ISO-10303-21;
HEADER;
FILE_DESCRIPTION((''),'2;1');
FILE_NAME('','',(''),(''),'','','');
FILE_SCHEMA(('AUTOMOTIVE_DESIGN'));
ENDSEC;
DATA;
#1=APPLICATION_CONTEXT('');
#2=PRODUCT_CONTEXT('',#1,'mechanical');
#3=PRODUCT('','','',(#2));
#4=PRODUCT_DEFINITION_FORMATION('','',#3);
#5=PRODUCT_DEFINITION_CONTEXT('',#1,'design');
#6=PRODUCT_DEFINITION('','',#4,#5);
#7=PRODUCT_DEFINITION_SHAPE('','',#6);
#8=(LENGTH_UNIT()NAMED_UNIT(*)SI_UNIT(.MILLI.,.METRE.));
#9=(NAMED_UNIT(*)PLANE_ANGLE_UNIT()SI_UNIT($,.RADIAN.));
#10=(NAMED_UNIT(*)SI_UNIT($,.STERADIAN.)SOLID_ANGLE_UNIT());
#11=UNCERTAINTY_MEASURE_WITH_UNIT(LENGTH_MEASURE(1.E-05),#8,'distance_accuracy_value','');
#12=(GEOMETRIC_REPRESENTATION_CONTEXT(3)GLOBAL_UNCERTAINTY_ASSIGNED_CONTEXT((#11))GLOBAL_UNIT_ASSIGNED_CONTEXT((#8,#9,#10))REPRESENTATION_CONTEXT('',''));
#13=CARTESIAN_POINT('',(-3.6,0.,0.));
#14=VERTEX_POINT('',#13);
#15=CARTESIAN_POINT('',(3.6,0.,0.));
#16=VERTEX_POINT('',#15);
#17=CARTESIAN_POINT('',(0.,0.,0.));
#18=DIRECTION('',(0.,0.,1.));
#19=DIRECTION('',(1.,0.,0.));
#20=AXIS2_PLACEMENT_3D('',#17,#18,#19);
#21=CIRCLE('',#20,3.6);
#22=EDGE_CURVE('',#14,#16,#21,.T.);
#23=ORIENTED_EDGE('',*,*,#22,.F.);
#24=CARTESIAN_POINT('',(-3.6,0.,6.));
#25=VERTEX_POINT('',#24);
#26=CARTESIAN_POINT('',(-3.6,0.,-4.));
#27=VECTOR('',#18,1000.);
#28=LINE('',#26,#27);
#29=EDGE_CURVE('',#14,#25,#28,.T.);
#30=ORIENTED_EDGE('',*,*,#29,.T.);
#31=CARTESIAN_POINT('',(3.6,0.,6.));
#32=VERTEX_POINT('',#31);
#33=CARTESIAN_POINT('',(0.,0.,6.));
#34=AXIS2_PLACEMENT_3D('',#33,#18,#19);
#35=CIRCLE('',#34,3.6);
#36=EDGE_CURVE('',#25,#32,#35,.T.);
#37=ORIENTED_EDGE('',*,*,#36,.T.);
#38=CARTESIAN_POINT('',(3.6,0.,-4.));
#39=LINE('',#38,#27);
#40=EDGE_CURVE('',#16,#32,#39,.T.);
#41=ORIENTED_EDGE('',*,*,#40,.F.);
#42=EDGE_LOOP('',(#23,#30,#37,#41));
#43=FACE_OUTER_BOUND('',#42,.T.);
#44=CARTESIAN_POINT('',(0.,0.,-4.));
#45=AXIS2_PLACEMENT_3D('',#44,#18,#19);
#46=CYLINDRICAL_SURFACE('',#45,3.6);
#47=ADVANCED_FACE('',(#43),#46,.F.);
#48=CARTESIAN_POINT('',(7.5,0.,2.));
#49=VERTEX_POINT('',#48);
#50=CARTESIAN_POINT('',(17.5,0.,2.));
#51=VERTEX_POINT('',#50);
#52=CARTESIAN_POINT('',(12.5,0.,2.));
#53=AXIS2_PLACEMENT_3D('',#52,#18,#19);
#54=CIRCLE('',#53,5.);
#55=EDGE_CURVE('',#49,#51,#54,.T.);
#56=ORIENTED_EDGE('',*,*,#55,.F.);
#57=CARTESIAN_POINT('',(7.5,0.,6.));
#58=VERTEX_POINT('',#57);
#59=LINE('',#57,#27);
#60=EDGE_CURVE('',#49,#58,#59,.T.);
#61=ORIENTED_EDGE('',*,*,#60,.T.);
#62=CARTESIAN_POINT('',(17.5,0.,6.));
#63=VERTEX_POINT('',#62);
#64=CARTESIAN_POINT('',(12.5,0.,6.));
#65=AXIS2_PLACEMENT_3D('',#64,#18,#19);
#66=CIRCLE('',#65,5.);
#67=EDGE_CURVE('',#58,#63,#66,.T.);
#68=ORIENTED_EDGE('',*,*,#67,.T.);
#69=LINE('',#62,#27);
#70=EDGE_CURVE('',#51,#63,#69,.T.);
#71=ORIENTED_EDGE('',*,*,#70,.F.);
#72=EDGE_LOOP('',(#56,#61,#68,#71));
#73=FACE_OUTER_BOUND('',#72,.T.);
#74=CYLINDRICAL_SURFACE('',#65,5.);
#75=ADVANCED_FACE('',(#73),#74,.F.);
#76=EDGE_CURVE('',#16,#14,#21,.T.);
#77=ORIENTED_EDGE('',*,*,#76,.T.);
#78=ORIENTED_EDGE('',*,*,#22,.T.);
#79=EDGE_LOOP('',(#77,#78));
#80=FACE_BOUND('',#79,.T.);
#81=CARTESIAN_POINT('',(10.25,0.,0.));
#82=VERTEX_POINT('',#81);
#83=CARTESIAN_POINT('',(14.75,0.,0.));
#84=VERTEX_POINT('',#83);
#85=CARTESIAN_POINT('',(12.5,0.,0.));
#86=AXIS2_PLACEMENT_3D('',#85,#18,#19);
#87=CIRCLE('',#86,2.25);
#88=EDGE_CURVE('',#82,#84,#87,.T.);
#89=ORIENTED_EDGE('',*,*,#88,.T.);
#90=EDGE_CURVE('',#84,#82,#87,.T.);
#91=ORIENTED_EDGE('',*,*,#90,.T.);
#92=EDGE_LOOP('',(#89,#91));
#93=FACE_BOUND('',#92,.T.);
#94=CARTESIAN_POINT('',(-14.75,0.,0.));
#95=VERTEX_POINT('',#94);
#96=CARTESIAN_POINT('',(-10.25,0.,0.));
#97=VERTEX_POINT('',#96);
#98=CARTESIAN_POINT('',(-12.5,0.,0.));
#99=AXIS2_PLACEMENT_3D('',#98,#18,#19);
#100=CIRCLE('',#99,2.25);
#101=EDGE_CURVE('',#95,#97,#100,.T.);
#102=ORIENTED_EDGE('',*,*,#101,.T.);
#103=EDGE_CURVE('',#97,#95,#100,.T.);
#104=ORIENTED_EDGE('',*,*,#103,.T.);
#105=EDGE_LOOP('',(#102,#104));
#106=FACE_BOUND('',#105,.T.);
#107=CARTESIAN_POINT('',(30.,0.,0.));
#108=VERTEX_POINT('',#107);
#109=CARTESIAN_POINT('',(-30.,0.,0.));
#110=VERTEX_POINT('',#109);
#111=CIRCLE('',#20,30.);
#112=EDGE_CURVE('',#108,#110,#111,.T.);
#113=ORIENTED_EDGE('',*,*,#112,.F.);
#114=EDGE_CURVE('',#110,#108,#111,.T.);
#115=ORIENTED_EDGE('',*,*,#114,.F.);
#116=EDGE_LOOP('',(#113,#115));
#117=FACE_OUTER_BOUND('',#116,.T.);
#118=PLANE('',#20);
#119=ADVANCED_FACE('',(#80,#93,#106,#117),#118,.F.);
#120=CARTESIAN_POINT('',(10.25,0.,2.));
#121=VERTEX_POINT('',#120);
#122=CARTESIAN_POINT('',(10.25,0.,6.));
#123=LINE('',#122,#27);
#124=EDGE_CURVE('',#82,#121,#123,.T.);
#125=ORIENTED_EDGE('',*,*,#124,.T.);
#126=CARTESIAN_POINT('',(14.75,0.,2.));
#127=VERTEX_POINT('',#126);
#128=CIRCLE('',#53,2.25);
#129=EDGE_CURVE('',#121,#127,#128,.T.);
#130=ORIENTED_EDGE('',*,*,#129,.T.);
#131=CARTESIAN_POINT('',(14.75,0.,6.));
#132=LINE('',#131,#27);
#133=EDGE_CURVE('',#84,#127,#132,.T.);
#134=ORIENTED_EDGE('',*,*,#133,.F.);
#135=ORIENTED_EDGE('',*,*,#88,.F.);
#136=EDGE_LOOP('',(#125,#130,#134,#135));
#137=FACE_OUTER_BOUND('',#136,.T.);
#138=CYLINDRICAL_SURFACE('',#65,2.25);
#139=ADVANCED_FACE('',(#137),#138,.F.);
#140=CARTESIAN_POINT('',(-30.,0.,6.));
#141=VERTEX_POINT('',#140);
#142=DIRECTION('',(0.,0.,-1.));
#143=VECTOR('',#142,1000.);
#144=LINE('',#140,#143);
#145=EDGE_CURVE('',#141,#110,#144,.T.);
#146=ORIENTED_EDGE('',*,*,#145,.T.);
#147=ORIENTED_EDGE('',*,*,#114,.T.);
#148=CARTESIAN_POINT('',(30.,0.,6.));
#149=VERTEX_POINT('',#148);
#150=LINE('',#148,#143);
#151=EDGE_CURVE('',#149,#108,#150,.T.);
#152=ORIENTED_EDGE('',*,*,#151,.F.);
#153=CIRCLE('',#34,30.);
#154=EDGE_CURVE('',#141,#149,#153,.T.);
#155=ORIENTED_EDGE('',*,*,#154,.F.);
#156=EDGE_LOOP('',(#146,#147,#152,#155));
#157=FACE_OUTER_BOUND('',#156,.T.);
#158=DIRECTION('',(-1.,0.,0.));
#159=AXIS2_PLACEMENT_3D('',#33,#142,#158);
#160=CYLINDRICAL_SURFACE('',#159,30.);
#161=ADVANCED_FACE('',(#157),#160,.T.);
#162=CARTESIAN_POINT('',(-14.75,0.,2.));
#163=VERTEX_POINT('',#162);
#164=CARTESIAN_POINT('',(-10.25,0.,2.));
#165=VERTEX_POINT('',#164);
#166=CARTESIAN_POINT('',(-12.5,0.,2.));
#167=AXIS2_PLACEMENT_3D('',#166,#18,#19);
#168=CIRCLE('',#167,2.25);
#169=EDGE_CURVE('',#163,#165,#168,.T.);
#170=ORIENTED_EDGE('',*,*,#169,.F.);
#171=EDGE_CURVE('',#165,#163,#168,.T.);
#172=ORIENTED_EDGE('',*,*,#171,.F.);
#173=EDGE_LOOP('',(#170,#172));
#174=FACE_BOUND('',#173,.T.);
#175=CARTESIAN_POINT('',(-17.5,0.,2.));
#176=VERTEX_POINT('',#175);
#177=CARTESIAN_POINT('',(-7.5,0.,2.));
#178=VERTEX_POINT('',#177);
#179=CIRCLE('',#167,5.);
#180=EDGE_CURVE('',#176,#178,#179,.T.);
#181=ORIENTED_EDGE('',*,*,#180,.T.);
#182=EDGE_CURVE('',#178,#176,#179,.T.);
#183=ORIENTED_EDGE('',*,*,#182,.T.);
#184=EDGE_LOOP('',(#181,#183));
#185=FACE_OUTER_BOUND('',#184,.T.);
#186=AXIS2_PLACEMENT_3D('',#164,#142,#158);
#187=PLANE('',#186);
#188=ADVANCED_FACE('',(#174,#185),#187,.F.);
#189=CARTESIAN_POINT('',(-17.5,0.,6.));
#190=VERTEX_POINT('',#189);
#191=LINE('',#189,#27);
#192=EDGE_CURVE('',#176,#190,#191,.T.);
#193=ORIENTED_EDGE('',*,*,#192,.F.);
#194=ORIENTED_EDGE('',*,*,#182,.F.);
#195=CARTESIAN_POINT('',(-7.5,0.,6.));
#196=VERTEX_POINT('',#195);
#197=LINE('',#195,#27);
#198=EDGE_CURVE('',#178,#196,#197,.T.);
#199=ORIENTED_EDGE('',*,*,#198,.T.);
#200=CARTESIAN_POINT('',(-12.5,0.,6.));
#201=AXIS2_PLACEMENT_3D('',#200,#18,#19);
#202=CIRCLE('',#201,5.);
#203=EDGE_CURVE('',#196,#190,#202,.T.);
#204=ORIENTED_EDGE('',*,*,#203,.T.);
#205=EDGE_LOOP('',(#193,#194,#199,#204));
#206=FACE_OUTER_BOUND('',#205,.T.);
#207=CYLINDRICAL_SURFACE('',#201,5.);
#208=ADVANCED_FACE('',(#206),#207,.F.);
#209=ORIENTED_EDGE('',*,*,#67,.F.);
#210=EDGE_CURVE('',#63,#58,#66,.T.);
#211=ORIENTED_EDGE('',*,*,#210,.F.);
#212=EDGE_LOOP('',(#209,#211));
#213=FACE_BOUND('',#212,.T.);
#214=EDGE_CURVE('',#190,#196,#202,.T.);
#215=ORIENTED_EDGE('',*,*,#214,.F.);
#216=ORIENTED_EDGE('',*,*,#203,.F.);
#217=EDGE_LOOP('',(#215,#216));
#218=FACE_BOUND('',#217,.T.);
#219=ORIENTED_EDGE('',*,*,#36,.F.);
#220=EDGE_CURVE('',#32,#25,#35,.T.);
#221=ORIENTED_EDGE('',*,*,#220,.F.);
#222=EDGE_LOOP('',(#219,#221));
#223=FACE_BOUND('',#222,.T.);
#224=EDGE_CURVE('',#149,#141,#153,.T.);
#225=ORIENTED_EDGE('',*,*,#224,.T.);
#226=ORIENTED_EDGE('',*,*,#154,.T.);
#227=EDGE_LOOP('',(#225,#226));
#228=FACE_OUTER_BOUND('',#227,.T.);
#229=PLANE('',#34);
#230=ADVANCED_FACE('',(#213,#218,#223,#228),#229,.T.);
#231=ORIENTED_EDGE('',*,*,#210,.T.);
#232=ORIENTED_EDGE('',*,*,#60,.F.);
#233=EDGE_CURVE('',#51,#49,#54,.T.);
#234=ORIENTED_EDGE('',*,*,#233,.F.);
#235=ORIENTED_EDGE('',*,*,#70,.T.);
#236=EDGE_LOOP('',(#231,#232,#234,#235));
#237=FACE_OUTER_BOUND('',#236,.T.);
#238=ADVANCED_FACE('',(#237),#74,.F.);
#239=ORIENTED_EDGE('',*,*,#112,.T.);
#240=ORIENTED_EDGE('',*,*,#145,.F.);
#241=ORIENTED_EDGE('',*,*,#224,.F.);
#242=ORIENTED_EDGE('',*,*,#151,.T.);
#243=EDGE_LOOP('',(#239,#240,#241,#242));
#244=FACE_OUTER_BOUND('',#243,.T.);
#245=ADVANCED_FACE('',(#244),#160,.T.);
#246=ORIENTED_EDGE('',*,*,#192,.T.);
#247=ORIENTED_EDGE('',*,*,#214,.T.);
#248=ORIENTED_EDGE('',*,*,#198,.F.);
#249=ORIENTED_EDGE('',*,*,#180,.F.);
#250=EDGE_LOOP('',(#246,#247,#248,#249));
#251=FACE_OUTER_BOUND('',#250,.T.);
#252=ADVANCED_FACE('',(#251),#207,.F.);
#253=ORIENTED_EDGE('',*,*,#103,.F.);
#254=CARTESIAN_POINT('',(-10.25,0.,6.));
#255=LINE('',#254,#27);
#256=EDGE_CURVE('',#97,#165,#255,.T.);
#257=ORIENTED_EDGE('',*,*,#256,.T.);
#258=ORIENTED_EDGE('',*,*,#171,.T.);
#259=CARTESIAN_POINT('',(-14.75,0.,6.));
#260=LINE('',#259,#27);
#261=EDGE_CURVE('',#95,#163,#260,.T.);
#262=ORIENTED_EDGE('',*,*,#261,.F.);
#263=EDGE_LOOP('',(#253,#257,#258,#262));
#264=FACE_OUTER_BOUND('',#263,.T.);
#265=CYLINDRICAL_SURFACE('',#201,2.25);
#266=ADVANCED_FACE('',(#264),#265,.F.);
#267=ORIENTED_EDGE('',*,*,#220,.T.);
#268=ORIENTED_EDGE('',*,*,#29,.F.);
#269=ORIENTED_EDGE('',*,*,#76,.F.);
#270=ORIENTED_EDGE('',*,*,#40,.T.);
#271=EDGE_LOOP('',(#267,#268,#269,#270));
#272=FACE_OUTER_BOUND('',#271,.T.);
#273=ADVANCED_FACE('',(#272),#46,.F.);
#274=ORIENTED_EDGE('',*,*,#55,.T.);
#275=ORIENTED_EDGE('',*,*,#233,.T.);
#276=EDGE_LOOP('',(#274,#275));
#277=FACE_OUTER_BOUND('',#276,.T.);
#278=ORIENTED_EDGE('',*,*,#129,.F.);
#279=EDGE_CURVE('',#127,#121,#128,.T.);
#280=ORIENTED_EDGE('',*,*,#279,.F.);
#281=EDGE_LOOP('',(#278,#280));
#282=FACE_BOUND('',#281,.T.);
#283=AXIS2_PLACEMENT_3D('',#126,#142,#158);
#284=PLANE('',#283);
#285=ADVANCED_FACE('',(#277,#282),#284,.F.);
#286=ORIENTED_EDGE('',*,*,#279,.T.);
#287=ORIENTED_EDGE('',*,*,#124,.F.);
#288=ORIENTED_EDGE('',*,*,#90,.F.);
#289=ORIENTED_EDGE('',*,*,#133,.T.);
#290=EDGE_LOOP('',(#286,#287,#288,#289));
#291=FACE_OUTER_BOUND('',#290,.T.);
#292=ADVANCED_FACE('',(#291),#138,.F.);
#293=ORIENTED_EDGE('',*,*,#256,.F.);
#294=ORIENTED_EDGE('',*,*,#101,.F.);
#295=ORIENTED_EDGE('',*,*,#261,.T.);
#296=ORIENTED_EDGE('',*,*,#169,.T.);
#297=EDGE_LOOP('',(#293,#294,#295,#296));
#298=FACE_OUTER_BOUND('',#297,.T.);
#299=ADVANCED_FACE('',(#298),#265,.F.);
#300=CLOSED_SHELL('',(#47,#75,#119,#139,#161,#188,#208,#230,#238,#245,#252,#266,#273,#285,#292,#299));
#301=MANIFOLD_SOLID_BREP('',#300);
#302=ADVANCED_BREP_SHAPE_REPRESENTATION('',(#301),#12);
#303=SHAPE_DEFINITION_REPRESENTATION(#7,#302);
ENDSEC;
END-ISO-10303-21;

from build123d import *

# Parameters (mm, degrees)
SKETCH1_R                               = 30
BOSS_EXTRUDE1_DEPTH                     = 6
CBORE_FOR_M4_HEX_HEAD_BOLT1_D           = 4.5
CBORE_FOR_M4_HEX_HEAD_BOLT1_CBORE_D     = 10
CBORE_FOR_M4_HEX_HEAD_BOLT1_CBORE_DEPTH = 4
SKETCH4_R                               = 3.6
CUT_EXTRUDE1_DEPTH                      = 10


with BuildPart() as part:
    # Sketch1 → Boss-Extrude1 (new body)
    with BuildSketch(Plane.XY):
        Circle(SKETCH1_R)
    extrude(amount=BOSS_EXTRUDE1_DEPTH)

    # CBORE for M4 Hex Head Bolt1 (through all)
    with Locations(Plane.XY.offset(6)):
        with Locations((-12.5, 0), (12.5, 0)):
            CounterBoreHole(CBORE_FOR_M4_HEX_HEAD_BOLT1_D / 2, CBORE_FOR_M4_HEX_HEAD_BOLT1_CBORE_D / 2, CBORE_FOR_M4_HEX_HEAD_BOLT1_CBORE_DEPTH)

    # Sketch4 → Cut-Extrude1 (cut)
    with BuildSketch(Plane.XY.offset(6)):
        Circle(SKETCH4_R)
    extrude(amount=-CUT_EXTRUDE1_DEPTH, mode=Mode.SUBTRACT)


solid = part.part
